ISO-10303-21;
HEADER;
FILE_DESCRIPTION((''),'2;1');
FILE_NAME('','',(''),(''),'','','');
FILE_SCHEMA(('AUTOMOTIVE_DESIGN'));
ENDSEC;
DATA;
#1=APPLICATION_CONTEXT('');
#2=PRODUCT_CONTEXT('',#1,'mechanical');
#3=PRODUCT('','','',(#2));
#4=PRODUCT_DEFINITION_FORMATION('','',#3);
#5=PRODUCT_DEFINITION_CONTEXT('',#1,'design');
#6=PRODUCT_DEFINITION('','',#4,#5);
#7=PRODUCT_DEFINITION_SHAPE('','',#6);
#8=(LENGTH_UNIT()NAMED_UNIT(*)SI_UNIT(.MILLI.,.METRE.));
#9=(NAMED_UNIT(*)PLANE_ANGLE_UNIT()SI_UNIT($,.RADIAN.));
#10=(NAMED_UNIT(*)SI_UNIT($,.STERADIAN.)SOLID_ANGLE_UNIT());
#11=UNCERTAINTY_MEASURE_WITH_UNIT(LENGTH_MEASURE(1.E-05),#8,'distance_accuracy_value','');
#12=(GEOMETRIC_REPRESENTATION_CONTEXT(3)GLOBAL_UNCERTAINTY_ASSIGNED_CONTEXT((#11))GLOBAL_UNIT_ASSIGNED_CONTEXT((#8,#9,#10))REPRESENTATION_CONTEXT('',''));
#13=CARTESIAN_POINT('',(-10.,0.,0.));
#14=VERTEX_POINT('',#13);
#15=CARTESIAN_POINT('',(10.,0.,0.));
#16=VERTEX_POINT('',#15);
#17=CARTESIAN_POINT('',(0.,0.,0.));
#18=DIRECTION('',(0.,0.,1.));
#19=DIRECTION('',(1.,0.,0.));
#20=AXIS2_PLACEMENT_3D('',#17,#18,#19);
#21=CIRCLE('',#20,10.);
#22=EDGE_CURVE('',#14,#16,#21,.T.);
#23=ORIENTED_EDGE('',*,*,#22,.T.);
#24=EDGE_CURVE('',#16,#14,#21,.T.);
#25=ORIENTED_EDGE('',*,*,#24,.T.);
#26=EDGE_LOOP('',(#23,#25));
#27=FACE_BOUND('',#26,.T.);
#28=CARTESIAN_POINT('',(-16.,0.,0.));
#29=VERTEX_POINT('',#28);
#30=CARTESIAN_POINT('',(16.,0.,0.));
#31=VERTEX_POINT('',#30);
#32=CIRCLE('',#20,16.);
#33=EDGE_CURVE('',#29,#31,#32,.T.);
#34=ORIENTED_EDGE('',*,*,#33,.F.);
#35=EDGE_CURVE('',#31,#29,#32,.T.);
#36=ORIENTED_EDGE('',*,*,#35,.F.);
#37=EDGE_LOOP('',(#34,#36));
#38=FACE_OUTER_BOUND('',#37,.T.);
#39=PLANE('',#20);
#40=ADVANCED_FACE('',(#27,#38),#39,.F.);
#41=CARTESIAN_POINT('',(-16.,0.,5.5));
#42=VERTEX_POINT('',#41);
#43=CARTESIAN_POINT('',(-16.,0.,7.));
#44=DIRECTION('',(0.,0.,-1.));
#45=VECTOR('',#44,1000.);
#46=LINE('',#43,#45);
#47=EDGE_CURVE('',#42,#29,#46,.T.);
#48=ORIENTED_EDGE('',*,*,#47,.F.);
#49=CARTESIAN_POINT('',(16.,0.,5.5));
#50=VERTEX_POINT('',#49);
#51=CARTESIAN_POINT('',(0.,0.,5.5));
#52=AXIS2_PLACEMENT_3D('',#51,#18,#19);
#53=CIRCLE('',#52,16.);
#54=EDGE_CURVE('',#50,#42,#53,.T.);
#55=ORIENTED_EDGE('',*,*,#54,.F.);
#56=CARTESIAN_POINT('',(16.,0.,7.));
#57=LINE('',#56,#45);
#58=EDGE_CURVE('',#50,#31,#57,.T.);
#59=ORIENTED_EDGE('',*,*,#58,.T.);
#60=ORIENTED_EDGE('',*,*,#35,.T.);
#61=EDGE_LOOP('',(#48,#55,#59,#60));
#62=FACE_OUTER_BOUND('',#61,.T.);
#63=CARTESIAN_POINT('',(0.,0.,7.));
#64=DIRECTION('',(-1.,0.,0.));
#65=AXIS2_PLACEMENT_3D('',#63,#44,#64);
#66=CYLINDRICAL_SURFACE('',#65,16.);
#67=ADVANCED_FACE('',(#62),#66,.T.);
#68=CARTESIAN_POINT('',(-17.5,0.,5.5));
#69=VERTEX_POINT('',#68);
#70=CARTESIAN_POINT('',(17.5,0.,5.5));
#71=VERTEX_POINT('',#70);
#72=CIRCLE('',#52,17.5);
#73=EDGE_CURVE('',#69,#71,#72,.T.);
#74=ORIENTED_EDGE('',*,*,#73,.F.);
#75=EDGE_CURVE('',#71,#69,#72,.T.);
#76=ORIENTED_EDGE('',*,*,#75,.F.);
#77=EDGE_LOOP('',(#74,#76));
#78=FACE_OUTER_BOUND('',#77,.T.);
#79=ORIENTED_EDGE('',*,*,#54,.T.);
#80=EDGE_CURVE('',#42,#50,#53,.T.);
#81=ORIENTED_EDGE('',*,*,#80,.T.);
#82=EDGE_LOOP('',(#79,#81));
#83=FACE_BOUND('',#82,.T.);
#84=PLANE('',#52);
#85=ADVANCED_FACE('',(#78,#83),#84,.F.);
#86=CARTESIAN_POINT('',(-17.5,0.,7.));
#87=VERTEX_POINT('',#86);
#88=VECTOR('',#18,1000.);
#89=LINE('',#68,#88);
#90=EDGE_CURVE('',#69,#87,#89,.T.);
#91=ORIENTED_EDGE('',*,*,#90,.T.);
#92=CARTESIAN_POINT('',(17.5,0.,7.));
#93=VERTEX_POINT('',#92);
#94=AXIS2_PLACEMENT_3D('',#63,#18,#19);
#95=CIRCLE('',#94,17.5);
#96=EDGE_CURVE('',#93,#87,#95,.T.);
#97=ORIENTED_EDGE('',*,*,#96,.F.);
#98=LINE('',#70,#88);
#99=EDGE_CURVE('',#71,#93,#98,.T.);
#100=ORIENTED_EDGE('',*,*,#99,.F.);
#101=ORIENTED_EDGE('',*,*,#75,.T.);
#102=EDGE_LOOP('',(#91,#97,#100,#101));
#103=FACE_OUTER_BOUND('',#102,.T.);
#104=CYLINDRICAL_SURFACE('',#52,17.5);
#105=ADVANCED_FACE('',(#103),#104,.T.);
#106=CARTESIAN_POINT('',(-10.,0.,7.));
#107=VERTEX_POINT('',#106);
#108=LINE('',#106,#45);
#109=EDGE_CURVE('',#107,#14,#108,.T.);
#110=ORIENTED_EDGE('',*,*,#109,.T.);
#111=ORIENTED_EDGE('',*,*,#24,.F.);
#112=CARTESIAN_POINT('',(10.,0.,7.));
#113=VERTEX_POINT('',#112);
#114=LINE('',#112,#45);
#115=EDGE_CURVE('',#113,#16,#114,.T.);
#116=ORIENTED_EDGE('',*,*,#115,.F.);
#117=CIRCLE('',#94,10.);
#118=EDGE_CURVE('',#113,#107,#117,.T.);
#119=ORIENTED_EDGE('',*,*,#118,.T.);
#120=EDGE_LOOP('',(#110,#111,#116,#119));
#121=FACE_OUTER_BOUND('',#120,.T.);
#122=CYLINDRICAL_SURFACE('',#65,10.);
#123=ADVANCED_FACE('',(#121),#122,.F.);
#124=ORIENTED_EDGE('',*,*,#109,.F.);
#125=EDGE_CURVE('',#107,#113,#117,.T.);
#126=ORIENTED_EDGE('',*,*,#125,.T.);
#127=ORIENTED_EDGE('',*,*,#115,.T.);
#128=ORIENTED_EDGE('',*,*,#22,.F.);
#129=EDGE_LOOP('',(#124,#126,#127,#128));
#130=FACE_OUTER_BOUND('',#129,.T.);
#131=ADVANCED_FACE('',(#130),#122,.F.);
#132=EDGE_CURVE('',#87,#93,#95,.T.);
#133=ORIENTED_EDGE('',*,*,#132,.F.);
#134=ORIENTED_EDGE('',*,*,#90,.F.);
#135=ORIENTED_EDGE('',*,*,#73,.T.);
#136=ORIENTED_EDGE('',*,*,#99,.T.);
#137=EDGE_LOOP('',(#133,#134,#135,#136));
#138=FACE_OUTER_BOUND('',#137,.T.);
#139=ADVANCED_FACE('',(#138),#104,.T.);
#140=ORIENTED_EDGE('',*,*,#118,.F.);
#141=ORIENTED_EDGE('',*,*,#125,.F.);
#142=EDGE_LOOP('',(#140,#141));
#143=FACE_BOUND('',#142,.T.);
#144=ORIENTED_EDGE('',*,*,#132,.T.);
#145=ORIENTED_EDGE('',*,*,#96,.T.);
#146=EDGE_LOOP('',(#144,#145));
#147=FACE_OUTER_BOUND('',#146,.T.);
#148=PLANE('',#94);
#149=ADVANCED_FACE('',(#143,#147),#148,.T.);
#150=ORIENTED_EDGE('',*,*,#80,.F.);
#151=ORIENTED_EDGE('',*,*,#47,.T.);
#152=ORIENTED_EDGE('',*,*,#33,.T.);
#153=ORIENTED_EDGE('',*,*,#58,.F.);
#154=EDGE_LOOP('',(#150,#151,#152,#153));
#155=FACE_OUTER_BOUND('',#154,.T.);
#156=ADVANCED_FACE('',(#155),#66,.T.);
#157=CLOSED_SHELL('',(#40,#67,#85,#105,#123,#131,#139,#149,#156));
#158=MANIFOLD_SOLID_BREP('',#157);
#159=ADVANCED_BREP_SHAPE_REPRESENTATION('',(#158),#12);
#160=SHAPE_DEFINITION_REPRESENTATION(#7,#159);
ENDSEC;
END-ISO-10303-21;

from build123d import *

# Parameters (mm, degrees)
SKETCH_1_R      = 16
SKETCH_1_R_2    = 10
EXTRUDE_1_DEPTH = 7
EXTRUDE_START   = -1.5
SKETCH_2_R      = 17.5
SKETCH_2_R_2    = 16
EXTRUDE_2_DEPTH = 1.5


with BuildPart() as part:
    # 草图1 → 凸台-拉伸1 (new body)
    with BuildSketch(Plane.XY):
        Circle(SKETCH_1_R)
        Circle(SKETCH_1_R_2, mode=Mode.SUBTRACT)
    extrude(amount=EXTRUDE_1_DEPTH)

    # 草图2 → 凸台-拉伸2 (add)
    with BuildSketch(Plane.XY.offset(7).offset(EXTRUDE_START)):
        Circle(SKETCH_2_R)
        Circle(SKETCH_2_R_2, mode=Mode.SUBTRACT)
    extrude(amount=EXTRUDE_2_DEPTH)


solid = part.part
